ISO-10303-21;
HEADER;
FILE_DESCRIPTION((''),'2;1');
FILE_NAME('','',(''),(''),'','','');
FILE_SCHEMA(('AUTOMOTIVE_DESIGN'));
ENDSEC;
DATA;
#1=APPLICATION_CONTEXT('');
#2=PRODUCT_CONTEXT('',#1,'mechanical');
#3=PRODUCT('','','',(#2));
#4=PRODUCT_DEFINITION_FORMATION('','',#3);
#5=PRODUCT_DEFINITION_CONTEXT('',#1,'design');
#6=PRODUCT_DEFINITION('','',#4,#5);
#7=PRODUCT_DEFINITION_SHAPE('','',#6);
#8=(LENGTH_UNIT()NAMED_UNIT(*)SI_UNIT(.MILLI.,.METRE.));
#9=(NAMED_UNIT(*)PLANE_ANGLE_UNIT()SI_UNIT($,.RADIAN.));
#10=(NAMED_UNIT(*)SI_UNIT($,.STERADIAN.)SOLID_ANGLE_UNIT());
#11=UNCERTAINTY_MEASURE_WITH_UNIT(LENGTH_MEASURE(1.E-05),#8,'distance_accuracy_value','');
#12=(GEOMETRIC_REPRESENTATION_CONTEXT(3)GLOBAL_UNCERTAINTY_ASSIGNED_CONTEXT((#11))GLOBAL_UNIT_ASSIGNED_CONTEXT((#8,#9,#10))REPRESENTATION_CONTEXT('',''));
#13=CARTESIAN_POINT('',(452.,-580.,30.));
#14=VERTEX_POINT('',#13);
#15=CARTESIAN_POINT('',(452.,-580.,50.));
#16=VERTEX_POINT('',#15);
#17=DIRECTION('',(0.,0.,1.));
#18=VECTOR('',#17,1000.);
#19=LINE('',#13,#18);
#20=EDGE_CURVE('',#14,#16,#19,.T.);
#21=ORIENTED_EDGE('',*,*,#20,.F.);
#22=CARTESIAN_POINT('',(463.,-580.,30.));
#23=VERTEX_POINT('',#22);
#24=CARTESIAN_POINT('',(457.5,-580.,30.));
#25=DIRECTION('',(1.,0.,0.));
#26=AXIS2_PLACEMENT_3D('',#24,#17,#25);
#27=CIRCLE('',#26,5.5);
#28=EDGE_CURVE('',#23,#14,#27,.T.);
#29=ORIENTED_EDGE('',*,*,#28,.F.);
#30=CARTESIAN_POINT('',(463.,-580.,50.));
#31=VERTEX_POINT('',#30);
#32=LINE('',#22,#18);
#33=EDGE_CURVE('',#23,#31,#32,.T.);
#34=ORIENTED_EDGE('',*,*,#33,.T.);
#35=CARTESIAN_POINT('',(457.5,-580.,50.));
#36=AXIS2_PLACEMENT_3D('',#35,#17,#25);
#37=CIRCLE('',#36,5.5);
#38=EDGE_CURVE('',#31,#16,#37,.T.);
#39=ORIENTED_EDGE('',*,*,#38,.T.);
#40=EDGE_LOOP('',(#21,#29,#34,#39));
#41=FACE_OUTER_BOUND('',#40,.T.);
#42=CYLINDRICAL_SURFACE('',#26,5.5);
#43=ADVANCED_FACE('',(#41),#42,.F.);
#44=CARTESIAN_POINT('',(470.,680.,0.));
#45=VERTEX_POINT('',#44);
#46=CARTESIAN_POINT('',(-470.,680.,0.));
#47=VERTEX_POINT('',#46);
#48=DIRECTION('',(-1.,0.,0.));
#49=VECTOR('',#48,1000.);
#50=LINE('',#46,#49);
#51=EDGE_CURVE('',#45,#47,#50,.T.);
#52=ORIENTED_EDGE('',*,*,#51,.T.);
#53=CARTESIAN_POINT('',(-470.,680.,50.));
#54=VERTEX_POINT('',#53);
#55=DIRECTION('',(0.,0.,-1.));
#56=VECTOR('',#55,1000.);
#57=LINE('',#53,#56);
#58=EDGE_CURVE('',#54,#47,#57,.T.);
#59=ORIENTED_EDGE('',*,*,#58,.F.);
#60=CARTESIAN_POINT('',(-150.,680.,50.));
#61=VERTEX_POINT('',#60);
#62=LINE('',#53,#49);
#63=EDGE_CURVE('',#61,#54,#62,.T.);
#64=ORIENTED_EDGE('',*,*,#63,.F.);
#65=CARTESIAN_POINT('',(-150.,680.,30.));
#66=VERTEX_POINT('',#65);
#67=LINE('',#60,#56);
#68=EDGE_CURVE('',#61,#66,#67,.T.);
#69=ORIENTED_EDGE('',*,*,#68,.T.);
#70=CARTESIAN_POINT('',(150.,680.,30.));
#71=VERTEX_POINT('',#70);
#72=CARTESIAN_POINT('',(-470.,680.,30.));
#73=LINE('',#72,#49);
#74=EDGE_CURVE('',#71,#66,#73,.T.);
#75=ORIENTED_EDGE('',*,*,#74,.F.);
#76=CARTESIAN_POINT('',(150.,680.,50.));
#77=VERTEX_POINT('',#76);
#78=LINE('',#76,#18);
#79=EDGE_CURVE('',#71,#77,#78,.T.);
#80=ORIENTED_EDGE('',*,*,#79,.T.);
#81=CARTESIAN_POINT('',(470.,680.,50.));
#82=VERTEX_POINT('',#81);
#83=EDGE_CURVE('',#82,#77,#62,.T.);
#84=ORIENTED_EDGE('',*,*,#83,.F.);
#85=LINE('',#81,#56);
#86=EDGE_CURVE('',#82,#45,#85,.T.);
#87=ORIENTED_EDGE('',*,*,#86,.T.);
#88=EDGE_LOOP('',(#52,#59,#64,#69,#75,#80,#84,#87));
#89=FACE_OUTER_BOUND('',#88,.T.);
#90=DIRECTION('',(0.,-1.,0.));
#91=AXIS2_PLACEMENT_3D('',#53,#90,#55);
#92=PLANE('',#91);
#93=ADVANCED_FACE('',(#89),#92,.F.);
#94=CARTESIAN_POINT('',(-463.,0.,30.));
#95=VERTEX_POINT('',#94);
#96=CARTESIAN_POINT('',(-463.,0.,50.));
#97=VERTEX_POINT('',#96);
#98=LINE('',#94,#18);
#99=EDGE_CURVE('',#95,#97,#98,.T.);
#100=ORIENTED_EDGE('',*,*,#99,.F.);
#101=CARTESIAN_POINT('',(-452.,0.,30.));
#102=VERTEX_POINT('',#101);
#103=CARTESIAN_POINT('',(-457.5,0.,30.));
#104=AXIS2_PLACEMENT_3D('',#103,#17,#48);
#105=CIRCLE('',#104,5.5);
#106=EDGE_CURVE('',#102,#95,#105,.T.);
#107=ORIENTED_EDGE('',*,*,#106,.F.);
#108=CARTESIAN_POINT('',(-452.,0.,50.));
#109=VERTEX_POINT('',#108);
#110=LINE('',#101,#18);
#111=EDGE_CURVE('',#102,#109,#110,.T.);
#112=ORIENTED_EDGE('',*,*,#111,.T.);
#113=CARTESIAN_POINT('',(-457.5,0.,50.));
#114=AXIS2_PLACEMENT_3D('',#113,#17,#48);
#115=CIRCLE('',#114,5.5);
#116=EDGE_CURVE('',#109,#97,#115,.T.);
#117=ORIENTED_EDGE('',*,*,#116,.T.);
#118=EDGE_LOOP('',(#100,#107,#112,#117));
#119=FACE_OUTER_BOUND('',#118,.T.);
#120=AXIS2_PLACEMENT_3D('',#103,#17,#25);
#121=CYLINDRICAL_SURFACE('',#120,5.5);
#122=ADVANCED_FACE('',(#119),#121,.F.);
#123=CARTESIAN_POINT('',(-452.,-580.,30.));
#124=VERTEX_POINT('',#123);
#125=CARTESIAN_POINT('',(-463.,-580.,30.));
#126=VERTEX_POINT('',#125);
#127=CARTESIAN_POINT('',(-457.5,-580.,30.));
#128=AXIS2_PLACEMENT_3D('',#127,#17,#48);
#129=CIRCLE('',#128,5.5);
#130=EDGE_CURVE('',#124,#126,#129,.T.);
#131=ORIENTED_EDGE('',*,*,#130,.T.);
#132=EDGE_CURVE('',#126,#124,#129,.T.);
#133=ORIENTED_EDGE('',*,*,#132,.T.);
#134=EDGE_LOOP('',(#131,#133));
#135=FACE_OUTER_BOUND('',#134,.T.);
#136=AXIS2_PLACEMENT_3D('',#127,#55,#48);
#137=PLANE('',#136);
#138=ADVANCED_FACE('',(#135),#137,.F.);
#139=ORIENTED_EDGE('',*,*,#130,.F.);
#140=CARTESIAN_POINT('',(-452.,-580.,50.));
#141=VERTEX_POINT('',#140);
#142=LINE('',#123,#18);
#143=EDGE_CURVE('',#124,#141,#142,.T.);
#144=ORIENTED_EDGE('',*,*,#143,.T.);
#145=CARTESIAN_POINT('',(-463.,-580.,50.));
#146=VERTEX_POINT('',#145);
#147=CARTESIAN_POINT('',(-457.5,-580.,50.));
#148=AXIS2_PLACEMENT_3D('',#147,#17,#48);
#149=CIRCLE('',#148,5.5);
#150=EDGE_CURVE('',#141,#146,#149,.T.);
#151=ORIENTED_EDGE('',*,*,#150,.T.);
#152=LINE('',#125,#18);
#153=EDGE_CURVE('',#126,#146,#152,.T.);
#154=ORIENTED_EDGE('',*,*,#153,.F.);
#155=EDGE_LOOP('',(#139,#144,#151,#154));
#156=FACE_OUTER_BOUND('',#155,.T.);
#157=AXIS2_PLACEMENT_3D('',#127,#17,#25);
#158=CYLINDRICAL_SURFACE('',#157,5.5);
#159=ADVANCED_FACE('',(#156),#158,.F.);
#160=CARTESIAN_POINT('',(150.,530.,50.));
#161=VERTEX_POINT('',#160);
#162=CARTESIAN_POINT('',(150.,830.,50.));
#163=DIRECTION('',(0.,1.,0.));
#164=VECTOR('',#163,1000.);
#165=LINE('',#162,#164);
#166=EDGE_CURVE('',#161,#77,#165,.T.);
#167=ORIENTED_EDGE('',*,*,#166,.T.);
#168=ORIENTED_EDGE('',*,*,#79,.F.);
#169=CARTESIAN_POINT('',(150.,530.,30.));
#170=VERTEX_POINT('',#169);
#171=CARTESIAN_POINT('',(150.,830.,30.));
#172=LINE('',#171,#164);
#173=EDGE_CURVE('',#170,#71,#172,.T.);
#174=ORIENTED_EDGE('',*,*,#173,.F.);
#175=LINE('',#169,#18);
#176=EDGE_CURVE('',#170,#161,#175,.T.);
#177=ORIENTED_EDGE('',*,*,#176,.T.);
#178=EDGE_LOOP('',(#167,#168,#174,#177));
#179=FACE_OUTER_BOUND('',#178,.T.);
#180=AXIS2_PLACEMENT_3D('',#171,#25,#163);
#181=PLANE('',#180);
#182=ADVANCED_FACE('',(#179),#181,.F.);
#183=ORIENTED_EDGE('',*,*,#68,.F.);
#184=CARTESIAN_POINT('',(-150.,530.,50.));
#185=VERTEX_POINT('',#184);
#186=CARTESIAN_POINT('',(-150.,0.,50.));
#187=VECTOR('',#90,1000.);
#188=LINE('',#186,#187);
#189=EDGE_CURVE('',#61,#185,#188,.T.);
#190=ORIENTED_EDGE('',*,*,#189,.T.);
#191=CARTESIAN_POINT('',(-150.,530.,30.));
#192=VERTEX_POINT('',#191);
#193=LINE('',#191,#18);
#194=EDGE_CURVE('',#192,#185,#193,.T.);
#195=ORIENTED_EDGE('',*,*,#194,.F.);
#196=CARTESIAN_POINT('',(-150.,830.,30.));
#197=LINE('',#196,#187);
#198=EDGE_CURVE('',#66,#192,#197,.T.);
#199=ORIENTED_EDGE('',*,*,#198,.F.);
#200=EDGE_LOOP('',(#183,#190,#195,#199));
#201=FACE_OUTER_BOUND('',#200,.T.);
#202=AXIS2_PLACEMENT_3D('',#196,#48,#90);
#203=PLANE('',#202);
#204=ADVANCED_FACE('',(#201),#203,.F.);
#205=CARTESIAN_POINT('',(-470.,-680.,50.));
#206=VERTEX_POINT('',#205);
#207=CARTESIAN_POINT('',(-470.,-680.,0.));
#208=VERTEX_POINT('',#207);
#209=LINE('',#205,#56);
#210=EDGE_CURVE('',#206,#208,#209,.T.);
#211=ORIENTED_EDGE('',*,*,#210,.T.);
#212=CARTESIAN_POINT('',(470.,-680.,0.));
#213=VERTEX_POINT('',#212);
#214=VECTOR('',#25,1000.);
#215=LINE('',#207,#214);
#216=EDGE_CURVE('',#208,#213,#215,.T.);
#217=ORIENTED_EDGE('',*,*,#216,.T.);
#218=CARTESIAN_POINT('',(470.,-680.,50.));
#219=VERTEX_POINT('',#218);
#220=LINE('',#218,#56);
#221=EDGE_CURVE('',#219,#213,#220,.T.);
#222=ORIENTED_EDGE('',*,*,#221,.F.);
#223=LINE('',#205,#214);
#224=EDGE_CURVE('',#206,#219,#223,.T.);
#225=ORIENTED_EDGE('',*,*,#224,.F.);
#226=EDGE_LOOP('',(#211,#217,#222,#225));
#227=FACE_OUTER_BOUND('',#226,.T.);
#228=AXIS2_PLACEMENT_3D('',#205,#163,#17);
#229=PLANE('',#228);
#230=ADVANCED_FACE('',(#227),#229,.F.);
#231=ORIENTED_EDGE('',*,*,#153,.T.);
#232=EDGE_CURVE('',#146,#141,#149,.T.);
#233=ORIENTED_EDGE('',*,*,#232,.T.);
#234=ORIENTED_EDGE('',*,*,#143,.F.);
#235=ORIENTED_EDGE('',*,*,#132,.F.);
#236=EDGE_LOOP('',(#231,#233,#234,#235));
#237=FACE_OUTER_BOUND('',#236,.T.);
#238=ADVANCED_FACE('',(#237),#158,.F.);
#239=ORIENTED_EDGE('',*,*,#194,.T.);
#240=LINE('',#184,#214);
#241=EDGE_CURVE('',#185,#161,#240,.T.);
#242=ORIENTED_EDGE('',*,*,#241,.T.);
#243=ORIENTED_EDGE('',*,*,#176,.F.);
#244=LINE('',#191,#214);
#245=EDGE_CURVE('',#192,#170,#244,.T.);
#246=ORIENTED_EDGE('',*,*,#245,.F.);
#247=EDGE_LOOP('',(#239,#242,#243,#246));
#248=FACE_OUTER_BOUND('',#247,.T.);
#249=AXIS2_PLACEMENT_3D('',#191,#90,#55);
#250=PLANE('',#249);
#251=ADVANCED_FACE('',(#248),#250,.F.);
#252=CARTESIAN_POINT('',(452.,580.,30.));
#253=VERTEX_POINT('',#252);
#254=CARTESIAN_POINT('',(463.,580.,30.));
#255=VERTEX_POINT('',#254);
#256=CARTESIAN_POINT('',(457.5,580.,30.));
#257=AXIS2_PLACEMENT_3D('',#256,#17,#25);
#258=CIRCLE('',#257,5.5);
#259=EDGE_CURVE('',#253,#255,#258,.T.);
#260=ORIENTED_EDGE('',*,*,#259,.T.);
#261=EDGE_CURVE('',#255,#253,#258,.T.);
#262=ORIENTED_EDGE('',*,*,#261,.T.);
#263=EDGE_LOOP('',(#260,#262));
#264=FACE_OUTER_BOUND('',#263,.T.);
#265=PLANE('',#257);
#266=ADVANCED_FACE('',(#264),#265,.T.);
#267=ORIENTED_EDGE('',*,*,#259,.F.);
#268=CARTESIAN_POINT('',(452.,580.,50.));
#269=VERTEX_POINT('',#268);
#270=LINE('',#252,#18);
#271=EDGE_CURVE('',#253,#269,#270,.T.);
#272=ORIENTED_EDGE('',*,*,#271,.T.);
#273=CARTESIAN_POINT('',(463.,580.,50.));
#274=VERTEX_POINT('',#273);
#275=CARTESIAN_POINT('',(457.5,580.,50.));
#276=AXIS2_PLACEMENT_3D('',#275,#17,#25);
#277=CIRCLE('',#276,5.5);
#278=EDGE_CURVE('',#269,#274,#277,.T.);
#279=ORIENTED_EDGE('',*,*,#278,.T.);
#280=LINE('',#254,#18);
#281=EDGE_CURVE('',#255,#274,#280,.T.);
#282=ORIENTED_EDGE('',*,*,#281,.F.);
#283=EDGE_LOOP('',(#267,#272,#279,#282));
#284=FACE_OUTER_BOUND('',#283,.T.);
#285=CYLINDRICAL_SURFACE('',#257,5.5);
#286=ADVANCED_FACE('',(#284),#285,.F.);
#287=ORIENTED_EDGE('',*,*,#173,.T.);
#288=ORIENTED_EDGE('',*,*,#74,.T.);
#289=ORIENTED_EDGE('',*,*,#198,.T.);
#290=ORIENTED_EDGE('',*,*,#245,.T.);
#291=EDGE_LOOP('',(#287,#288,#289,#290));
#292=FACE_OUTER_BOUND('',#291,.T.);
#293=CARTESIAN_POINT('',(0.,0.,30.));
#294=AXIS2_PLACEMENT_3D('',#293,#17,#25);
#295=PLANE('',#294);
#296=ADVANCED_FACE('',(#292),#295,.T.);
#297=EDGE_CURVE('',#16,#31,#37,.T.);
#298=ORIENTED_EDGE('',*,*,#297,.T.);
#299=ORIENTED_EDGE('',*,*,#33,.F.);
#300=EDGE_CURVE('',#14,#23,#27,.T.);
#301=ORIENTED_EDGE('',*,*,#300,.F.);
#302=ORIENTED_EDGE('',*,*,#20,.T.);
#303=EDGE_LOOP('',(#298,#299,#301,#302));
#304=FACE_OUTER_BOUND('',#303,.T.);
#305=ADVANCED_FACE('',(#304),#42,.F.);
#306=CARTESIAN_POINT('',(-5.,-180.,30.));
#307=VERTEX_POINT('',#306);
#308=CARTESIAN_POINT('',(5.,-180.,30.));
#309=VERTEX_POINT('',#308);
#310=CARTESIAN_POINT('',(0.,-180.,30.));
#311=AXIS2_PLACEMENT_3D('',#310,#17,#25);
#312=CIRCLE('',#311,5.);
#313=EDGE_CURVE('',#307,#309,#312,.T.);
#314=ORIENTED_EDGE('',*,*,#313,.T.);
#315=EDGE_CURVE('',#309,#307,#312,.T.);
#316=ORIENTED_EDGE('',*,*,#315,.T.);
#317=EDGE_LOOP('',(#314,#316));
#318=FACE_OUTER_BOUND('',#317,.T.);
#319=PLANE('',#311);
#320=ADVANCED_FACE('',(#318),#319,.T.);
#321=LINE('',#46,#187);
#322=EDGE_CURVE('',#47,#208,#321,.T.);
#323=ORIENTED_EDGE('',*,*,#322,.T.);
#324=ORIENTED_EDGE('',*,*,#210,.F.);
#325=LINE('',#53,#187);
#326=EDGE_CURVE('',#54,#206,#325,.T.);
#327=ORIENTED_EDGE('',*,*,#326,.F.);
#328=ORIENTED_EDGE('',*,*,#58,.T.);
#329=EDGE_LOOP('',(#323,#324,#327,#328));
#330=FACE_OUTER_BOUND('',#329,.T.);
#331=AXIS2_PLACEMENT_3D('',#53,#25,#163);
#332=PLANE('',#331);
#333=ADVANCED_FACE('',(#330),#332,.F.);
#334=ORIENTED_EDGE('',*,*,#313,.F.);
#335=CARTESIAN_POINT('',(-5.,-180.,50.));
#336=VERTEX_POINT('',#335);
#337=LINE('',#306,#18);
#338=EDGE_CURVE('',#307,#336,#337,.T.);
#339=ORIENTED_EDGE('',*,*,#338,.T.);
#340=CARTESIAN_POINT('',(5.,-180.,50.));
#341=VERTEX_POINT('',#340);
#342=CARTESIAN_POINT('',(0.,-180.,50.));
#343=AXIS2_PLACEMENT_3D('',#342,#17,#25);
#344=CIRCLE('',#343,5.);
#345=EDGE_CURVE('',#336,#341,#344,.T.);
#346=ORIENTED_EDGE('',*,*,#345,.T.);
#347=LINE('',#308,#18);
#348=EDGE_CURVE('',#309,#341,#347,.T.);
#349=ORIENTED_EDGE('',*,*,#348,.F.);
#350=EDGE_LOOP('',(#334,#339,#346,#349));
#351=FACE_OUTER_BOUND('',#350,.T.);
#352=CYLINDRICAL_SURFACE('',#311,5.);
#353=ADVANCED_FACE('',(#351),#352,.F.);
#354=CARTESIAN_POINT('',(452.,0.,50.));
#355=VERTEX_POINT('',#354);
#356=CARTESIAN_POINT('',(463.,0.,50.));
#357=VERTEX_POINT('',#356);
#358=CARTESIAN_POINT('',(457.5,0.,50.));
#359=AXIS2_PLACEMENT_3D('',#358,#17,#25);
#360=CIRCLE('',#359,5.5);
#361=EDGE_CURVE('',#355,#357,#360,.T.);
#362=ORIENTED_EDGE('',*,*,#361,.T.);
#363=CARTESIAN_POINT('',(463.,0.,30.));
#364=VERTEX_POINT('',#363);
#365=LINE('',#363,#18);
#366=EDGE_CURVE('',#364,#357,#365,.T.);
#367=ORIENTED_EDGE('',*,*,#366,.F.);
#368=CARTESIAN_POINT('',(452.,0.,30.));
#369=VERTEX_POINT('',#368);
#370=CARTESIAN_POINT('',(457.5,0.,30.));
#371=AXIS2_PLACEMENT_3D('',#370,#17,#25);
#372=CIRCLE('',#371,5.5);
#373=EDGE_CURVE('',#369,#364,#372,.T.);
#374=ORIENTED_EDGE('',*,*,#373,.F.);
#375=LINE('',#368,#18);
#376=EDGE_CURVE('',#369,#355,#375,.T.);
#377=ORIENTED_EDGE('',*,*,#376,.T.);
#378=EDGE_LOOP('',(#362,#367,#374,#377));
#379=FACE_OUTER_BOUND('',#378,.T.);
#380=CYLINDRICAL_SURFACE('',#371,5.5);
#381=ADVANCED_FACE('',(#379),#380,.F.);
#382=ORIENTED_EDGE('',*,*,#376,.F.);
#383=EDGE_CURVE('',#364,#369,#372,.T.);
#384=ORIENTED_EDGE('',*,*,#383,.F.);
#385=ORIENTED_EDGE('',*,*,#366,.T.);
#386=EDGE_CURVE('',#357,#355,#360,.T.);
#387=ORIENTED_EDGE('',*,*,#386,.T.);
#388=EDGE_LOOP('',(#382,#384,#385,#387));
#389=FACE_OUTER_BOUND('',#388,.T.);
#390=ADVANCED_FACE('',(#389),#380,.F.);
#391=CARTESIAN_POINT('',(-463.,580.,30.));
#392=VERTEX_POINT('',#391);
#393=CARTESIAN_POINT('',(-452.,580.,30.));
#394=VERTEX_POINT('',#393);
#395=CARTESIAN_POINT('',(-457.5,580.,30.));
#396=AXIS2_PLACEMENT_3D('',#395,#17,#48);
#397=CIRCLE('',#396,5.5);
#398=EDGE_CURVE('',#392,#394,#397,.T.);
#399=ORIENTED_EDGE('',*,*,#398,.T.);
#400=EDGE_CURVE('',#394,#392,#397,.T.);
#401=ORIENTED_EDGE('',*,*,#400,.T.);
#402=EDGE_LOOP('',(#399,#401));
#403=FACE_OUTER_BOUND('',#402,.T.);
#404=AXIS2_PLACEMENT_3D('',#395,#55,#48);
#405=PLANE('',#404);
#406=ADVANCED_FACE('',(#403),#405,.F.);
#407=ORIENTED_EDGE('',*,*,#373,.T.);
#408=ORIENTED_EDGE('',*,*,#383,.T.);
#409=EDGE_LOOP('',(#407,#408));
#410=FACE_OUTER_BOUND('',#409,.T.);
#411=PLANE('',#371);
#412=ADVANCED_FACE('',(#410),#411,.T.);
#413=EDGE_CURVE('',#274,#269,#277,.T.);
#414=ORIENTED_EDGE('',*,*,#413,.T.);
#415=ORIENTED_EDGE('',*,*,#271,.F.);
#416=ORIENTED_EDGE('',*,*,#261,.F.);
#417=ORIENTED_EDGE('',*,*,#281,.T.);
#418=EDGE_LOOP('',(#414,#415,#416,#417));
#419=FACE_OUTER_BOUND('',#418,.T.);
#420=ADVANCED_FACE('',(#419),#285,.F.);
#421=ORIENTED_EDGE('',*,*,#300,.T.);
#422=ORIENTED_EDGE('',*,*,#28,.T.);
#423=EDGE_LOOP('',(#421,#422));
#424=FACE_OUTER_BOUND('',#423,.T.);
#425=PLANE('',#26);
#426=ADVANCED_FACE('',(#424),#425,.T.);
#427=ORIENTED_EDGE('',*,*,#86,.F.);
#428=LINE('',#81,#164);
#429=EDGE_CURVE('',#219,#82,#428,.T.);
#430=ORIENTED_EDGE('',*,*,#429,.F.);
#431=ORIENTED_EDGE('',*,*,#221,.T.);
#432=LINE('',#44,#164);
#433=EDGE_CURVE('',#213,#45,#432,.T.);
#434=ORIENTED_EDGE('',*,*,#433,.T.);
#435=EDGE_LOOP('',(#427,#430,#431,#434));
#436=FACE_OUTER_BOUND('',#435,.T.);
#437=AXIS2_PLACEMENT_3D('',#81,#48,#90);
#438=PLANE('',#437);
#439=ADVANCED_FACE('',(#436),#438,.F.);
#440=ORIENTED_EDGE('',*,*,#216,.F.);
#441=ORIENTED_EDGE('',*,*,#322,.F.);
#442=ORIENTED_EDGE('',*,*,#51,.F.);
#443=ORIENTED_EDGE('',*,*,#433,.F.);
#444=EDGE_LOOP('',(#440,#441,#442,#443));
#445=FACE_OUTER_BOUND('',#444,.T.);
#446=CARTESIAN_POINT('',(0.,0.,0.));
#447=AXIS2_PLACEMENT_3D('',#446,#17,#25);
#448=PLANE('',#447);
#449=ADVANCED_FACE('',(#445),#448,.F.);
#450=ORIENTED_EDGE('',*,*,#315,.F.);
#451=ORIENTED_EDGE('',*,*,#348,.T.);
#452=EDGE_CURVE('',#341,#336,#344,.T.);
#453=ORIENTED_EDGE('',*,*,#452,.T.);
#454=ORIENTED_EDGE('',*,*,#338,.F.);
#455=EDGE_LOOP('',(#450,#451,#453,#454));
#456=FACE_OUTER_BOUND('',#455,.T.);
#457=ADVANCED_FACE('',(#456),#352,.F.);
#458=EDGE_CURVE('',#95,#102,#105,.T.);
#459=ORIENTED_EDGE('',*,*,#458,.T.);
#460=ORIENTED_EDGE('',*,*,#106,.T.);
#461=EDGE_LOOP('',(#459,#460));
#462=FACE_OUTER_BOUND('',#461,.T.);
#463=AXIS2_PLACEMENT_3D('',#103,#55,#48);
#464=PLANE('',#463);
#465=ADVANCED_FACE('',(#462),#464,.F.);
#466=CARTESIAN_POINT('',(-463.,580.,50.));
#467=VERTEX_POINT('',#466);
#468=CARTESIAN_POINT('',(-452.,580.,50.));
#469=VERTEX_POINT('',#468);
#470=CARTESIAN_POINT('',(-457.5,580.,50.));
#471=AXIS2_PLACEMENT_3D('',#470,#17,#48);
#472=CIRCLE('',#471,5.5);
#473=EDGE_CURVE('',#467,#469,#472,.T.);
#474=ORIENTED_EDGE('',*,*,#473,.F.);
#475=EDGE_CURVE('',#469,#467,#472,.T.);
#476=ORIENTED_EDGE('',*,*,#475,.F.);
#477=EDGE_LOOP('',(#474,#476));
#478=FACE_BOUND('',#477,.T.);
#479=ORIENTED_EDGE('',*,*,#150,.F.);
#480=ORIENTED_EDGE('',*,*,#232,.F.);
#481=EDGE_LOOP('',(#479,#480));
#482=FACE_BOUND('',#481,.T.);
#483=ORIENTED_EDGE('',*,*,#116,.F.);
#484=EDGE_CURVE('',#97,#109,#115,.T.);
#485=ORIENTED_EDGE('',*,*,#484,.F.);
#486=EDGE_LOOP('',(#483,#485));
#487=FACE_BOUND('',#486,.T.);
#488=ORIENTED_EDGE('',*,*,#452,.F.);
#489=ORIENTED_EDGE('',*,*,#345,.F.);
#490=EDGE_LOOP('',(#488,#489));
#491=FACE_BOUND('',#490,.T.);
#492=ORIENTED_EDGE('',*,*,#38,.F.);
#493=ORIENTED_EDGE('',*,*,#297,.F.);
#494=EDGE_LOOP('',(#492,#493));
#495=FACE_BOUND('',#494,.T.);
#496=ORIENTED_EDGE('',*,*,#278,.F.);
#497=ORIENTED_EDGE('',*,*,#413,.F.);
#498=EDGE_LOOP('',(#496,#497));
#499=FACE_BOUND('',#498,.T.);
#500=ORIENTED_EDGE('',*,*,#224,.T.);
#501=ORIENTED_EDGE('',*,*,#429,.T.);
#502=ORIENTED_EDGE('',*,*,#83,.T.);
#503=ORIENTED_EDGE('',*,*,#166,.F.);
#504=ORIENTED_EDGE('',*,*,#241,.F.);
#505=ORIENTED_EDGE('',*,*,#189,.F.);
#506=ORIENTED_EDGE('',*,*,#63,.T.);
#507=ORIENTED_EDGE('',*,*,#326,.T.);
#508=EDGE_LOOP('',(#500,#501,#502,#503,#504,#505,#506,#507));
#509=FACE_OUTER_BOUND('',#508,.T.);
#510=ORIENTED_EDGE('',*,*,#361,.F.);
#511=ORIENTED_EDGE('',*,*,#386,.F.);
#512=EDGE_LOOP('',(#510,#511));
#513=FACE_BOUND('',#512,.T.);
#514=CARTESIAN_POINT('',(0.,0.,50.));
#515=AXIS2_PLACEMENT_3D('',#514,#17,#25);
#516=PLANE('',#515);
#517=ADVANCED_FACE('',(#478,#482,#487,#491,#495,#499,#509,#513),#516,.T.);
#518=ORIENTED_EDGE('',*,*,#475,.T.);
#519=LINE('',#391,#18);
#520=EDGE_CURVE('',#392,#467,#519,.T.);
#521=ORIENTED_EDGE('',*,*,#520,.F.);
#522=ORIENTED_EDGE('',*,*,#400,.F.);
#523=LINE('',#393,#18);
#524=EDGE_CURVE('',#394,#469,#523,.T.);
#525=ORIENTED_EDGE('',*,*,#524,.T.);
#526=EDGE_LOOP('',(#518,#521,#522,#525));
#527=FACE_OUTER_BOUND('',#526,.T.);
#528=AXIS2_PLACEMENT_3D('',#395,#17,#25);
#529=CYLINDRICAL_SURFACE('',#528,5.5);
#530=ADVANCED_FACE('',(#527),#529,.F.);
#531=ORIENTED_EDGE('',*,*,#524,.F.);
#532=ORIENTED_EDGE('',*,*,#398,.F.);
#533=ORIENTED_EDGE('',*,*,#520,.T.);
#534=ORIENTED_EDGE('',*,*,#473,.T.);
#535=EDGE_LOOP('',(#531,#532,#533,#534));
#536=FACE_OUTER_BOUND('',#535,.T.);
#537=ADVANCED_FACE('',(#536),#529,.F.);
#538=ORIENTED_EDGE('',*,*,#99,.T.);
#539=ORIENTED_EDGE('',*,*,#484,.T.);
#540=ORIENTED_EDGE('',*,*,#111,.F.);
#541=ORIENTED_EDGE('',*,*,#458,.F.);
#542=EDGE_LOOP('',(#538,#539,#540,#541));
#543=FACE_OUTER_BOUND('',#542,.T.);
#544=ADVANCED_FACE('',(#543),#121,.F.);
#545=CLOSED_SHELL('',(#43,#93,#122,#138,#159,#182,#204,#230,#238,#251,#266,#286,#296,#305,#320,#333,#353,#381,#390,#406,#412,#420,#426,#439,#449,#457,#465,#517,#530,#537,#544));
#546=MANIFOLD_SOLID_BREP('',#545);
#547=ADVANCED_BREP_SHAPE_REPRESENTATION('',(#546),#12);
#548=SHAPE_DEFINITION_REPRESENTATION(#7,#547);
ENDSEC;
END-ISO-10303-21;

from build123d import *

# Parameters (mm, degrees)
SKETCH_1_W            = 940
SKETCH_1_H            = 1360
EXTRUDE_1_DEPTH       = 50
SKETCH_2_R            = 5
SKETCH_2_R_2          = 5.5
SKETCH_2_W            = 300
SKETCH_2_H            = 300
CUT_EXTRUDE_986_DEPTH = 20


with BuildPart() as part:
    # 草图1 → 凸台-拉伸1 (new body)
    with BuildSketch(Plane.XY):
        Rectangle(SKETCH_1_W, SKETCH_1_H)
    extrude(amount=EXTRUDE_1_DEPTH)

    # 草图2 → Cut-Extrude 986 (cut)
    with BuildSketch(Plane.XY.offset(50)):
        with Locations((0, -180)):
            Circle(SKETCH_2_R)
        with Locations((457.5, -580)):
            Circle(SKETCH_2_R_2)
        with Locations((457.5, 0)):
            Circle(SKETCH_2_R_2)
        with Locations((457.5, 580)):
            Circle(SKETCH_2_R_2)
        with Locations(Location((-457.5, 580, 0), (0, 0, 180))):
            Circle(SKETCH_2_R_2)
        with Locations(Location((-457.5, 0, 0), (0, 0, 180))):
            Circle(SKETCH_2_R_2)
        with Locations(Location((-457.5, -580, 0), (0, 0, 180))):
            Circle(SKETCH_2_R_2)
        with Locations((0, 680)):
            Rectangle(SKETCH_2_W, SKETCH_2_H)
    extrude(amount=-CUT_EXTRUDE_986_DEPTH, mode=Mode.SUBTRACT)


solid = part.part
